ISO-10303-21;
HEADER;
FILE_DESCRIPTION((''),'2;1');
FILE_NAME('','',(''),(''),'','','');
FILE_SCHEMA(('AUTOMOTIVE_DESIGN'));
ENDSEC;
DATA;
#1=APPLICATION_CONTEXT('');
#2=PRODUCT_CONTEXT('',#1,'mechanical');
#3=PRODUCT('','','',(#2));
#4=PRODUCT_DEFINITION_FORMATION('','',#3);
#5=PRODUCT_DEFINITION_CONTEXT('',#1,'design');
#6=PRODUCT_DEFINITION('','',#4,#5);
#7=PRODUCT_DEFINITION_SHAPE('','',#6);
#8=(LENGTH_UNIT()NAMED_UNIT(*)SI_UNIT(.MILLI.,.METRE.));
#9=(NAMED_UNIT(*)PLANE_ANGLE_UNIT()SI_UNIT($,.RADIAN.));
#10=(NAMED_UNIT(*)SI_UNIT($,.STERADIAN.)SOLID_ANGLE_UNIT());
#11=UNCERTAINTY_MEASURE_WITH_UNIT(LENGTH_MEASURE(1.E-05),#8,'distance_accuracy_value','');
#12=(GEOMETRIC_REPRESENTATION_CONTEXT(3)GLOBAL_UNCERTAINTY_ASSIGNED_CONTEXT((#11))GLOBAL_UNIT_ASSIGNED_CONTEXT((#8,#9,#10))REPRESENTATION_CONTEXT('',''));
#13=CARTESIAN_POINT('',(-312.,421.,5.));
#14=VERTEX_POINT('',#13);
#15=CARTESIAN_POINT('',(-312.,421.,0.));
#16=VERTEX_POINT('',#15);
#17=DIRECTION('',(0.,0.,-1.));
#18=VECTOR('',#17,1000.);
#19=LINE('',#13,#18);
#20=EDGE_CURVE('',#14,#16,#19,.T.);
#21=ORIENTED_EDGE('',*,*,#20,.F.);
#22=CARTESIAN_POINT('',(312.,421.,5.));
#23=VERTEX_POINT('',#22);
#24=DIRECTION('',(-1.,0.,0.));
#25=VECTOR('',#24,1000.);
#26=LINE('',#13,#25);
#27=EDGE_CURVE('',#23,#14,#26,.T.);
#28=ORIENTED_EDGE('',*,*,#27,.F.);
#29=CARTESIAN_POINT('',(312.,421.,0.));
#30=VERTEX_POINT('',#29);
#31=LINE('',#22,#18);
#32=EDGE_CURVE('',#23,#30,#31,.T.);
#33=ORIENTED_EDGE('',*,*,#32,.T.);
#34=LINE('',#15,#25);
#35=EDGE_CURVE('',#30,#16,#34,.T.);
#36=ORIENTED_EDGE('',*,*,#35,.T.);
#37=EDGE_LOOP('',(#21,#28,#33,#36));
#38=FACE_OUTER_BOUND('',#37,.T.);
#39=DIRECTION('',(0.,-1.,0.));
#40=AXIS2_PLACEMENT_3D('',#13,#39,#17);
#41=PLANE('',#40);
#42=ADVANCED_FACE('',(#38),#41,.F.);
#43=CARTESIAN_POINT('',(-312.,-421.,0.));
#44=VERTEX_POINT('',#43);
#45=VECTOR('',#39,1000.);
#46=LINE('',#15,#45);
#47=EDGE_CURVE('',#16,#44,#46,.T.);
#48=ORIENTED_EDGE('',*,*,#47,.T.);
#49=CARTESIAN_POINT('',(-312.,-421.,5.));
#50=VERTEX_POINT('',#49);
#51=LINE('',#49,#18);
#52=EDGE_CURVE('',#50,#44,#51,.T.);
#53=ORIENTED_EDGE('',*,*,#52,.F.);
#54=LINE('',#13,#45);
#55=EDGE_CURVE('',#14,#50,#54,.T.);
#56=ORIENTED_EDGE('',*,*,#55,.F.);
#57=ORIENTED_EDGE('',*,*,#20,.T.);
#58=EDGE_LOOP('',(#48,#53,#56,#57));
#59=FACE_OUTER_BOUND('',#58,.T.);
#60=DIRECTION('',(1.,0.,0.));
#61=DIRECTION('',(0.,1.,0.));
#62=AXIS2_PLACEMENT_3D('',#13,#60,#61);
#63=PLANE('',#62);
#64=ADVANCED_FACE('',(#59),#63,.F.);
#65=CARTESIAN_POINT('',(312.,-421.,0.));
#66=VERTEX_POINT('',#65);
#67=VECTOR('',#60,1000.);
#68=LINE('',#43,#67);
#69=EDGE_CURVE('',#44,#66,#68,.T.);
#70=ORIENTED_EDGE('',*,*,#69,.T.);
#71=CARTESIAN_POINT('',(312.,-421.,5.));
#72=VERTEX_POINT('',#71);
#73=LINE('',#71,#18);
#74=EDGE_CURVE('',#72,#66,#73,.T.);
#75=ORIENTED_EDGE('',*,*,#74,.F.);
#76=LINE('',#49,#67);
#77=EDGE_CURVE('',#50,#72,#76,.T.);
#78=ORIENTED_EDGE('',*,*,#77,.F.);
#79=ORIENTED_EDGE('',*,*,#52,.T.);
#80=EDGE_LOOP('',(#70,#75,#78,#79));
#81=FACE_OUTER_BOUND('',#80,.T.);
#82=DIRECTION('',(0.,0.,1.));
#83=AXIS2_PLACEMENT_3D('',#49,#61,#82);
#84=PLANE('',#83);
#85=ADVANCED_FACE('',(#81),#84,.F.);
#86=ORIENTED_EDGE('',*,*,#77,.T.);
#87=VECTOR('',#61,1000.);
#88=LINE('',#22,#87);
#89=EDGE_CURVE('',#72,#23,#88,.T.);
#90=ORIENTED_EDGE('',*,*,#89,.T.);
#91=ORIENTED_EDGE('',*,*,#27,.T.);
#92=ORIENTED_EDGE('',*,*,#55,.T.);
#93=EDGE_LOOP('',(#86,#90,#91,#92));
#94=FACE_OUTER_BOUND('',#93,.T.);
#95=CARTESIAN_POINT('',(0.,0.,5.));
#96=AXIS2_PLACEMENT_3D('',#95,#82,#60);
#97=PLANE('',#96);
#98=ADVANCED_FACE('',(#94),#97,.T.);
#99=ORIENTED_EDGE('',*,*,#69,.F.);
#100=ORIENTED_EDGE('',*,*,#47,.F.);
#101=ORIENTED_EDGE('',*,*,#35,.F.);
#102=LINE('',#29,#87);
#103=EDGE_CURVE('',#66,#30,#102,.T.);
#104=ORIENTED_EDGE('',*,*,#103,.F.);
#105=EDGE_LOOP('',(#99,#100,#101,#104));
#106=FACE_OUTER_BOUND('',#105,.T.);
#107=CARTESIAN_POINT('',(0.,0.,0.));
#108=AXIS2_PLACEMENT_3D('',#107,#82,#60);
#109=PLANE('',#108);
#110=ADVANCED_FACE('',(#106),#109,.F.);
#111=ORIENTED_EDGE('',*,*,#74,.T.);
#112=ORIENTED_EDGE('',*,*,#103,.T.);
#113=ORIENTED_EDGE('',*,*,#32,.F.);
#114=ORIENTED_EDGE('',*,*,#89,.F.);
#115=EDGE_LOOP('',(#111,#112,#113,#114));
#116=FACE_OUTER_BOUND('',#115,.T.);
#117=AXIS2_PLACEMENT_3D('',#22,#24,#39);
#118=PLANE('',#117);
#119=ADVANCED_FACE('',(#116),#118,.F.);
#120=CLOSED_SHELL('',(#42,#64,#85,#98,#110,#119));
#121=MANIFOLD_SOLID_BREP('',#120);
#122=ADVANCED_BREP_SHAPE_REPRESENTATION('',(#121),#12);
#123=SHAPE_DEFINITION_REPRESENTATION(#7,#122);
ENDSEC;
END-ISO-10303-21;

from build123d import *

# Parameters (mm, degrees)
SKETCH_1_W      = 624
SKETCH_1_H      = 842
EXTRUDE_1_DEPTH = 5


with BuildPart() as part:
    # 草图1 → 凸台-拉伸1 (new body)
    with BuildSketch(Plane.XY):
        Rectangle(SKETCH_1_W, SKETCH_1_H)
    extrude(amount=EXTRUDE_1_DEPTH)


solid = part.part
